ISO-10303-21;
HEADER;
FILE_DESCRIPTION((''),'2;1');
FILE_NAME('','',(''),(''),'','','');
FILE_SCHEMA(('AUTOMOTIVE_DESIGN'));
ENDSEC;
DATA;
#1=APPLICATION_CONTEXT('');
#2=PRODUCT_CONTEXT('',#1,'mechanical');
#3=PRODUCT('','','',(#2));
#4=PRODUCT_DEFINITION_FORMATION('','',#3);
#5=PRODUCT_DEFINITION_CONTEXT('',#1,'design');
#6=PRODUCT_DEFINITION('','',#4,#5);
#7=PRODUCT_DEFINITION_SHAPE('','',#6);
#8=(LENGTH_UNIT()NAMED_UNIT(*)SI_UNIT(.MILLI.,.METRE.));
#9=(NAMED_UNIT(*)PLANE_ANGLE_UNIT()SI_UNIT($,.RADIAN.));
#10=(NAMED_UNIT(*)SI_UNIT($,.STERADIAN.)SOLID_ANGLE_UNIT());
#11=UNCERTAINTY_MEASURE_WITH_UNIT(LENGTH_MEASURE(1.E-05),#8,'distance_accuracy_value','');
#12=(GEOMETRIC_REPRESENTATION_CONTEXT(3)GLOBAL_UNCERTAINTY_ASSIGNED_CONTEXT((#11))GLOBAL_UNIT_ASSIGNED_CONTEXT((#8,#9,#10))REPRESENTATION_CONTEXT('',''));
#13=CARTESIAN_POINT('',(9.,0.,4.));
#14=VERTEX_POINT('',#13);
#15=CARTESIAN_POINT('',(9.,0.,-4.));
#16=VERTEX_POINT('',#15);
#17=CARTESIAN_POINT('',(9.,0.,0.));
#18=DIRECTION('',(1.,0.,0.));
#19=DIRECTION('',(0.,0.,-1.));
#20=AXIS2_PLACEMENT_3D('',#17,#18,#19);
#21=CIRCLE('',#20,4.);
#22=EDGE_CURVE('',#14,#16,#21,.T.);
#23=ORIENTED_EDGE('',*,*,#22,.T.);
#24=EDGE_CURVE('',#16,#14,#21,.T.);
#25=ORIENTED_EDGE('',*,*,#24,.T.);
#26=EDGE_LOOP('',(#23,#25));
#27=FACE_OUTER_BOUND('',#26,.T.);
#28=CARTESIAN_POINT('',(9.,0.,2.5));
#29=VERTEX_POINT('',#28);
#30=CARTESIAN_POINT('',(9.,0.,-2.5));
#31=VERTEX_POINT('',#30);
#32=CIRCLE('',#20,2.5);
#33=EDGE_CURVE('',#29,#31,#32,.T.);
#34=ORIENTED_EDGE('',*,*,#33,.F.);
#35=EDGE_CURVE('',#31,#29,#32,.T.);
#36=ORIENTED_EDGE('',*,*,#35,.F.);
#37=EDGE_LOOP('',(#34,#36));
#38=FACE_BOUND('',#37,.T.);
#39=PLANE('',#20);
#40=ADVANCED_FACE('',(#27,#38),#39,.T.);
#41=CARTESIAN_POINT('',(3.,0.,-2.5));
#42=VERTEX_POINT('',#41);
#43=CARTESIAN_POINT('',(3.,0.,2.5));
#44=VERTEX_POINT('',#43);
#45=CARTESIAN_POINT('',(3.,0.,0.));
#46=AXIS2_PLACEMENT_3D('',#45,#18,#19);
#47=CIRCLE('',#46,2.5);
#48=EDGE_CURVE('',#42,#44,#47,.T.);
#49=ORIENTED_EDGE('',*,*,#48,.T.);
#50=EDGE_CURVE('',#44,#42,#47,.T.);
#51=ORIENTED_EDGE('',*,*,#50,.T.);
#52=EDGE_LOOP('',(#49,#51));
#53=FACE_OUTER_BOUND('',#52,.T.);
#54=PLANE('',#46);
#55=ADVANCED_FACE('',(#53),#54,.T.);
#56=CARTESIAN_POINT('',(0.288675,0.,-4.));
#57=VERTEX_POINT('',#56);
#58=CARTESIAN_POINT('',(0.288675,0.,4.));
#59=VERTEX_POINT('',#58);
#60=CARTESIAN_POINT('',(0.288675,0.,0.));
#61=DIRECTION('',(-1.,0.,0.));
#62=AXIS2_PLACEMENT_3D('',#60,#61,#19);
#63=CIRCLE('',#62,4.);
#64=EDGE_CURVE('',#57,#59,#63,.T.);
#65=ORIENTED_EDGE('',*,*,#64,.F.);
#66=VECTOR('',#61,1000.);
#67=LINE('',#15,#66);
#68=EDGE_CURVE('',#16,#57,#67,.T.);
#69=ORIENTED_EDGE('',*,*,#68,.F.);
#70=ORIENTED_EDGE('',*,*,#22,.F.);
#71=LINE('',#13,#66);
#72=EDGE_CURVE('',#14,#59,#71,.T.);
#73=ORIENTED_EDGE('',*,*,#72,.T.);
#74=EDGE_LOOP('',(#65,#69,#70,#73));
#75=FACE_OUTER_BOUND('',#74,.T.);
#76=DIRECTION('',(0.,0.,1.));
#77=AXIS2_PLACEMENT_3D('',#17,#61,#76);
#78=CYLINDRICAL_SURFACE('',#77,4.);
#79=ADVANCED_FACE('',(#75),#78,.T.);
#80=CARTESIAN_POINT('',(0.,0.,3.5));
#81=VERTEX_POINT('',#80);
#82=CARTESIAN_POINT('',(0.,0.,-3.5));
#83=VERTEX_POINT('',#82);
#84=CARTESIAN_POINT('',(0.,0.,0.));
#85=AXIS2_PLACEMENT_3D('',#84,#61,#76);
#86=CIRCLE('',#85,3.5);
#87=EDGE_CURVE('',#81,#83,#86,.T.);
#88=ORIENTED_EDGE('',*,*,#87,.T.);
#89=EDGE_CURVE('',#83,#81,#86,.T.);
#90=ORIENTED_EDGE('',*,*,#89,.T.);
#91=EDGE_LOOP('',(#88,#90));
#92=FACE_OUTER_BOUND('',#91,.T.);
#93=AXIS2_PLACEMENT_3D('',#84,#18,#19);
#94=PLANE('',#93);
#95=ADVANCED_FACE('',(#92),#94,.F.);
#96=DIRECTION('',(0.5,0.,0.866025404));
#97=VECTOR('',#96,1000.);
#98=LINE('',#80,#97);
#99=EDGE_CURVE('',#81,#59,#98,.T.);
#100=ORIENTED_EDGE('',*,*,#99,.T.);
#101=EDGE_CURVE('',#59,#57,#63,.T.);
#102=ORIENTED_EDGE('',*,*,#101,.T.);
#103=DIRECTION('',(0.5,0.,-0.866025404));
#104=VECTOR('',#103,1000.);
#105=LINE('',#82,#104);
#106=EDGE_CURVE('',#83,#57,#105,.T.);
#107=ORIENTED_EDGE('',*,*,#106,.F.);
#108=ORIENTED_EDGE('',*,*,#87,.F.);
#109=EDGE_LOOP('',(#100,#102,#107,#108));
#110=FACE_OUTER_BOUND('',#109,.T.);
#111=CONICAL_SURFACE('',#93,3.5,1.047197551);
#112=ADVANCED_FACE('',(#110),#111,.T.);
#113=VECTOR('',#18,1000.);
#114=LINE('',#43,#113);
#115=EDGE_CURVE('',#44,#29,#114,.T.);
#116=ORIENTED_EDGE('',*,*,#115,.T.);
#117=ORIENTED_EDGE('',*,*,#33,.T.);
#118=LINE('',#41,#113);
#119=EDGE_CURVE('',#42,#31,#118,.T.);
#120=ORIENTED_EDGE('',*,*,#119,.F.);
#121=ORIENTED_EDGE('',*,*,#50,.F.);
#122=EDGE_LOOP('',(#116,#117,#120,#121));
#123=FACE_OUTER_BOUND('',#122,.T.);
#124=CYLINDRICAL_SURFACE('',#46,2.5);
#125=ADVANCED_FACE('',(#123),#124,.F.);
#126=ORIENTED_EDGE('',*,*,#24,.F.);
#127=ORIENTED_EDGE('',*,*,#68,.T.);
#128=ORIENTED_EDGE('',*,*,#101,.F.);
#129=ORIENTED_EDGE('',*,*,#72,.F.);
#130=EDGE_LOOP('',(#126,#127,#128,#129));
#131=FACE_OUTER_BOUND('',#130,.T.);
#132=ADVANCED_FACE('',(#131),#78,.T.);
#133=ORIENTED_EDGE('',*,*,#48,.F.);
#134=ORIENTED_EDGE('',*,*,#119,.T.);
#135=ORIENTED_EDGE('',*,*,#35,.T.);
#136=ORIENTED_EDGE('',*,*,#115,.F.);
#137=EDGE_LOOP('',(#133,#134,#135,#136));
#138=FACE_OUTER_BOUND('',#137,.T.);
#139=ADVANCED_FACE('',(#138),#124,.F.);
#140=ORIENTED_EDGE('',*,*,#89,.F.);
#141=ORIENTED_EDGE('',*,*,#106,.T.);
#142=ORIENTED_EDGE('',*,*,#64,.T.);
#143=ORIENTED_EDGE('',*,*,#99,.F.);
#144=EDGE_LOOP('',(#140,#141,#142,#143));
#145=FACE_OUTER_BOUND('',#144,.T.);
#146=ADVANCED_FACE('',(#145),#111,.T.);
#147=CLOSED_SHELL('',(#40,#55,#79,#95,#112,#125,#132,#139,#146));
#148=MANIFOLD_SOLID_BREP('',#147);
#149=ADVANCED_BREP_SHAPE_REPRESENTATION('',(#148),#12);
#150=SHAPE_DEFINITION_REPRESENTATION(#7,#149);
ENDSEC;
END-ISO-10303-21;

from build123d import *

# Parameters (mm, degrees)
CAP_BODY_SKETCH_8_R = 4
CAP_BODY_8X9_DEPTH  = 9
BORE_SKETCH_5_R     = 2.5
BORE_5X6_DEPTH      = 6


with BuildPart() as part:
    # Cap Body Sketch Ø8 → Cap Body Ø8x9 (new body)
    with BuildSketch(Plane(origin=(0, 0, 0), x_dir=(0, 0, -1), z_dir=(1, 0, 0))):
        Circle(CAP_BODY_SKETCH_8_R)
    extrude(amount=CAP_BODY_8X9_DEPTH)

    # Bore Drill Point Sketch → Bore Drill Point Cut (revolve, cut)
    with BuildSketch(Plane.XY, mode=Mode.PRIVATE) as bore_drill_point_cut_sk:
        Polygon((0, 3.5), (0.700208968, 4.712797508), (0, 4.712797508), align=None)
    revolve(bore_drill_point_cut_sk.sketch.rotate(Axis((-1000, 0, 0), (1, 0, 0)), 270), axis=Axis((-1000, 0, 0), (1, 0, 0)), mode=Mode.SUBTRACT)

    # Bore Sketch Ø5 → Bore Ø5x6 (cut)
    with BuildSketch(Plane(origin=(9, 0, 0), x_dir=(0, 0, -1), z_dir=(1, 0, 0))):
        Circle(BORE_SKETCH_5_R)
    extrude(amount=-BORE_5X6_DEPTH, mode=Mode.SUBTRACT)


solid = part.part
